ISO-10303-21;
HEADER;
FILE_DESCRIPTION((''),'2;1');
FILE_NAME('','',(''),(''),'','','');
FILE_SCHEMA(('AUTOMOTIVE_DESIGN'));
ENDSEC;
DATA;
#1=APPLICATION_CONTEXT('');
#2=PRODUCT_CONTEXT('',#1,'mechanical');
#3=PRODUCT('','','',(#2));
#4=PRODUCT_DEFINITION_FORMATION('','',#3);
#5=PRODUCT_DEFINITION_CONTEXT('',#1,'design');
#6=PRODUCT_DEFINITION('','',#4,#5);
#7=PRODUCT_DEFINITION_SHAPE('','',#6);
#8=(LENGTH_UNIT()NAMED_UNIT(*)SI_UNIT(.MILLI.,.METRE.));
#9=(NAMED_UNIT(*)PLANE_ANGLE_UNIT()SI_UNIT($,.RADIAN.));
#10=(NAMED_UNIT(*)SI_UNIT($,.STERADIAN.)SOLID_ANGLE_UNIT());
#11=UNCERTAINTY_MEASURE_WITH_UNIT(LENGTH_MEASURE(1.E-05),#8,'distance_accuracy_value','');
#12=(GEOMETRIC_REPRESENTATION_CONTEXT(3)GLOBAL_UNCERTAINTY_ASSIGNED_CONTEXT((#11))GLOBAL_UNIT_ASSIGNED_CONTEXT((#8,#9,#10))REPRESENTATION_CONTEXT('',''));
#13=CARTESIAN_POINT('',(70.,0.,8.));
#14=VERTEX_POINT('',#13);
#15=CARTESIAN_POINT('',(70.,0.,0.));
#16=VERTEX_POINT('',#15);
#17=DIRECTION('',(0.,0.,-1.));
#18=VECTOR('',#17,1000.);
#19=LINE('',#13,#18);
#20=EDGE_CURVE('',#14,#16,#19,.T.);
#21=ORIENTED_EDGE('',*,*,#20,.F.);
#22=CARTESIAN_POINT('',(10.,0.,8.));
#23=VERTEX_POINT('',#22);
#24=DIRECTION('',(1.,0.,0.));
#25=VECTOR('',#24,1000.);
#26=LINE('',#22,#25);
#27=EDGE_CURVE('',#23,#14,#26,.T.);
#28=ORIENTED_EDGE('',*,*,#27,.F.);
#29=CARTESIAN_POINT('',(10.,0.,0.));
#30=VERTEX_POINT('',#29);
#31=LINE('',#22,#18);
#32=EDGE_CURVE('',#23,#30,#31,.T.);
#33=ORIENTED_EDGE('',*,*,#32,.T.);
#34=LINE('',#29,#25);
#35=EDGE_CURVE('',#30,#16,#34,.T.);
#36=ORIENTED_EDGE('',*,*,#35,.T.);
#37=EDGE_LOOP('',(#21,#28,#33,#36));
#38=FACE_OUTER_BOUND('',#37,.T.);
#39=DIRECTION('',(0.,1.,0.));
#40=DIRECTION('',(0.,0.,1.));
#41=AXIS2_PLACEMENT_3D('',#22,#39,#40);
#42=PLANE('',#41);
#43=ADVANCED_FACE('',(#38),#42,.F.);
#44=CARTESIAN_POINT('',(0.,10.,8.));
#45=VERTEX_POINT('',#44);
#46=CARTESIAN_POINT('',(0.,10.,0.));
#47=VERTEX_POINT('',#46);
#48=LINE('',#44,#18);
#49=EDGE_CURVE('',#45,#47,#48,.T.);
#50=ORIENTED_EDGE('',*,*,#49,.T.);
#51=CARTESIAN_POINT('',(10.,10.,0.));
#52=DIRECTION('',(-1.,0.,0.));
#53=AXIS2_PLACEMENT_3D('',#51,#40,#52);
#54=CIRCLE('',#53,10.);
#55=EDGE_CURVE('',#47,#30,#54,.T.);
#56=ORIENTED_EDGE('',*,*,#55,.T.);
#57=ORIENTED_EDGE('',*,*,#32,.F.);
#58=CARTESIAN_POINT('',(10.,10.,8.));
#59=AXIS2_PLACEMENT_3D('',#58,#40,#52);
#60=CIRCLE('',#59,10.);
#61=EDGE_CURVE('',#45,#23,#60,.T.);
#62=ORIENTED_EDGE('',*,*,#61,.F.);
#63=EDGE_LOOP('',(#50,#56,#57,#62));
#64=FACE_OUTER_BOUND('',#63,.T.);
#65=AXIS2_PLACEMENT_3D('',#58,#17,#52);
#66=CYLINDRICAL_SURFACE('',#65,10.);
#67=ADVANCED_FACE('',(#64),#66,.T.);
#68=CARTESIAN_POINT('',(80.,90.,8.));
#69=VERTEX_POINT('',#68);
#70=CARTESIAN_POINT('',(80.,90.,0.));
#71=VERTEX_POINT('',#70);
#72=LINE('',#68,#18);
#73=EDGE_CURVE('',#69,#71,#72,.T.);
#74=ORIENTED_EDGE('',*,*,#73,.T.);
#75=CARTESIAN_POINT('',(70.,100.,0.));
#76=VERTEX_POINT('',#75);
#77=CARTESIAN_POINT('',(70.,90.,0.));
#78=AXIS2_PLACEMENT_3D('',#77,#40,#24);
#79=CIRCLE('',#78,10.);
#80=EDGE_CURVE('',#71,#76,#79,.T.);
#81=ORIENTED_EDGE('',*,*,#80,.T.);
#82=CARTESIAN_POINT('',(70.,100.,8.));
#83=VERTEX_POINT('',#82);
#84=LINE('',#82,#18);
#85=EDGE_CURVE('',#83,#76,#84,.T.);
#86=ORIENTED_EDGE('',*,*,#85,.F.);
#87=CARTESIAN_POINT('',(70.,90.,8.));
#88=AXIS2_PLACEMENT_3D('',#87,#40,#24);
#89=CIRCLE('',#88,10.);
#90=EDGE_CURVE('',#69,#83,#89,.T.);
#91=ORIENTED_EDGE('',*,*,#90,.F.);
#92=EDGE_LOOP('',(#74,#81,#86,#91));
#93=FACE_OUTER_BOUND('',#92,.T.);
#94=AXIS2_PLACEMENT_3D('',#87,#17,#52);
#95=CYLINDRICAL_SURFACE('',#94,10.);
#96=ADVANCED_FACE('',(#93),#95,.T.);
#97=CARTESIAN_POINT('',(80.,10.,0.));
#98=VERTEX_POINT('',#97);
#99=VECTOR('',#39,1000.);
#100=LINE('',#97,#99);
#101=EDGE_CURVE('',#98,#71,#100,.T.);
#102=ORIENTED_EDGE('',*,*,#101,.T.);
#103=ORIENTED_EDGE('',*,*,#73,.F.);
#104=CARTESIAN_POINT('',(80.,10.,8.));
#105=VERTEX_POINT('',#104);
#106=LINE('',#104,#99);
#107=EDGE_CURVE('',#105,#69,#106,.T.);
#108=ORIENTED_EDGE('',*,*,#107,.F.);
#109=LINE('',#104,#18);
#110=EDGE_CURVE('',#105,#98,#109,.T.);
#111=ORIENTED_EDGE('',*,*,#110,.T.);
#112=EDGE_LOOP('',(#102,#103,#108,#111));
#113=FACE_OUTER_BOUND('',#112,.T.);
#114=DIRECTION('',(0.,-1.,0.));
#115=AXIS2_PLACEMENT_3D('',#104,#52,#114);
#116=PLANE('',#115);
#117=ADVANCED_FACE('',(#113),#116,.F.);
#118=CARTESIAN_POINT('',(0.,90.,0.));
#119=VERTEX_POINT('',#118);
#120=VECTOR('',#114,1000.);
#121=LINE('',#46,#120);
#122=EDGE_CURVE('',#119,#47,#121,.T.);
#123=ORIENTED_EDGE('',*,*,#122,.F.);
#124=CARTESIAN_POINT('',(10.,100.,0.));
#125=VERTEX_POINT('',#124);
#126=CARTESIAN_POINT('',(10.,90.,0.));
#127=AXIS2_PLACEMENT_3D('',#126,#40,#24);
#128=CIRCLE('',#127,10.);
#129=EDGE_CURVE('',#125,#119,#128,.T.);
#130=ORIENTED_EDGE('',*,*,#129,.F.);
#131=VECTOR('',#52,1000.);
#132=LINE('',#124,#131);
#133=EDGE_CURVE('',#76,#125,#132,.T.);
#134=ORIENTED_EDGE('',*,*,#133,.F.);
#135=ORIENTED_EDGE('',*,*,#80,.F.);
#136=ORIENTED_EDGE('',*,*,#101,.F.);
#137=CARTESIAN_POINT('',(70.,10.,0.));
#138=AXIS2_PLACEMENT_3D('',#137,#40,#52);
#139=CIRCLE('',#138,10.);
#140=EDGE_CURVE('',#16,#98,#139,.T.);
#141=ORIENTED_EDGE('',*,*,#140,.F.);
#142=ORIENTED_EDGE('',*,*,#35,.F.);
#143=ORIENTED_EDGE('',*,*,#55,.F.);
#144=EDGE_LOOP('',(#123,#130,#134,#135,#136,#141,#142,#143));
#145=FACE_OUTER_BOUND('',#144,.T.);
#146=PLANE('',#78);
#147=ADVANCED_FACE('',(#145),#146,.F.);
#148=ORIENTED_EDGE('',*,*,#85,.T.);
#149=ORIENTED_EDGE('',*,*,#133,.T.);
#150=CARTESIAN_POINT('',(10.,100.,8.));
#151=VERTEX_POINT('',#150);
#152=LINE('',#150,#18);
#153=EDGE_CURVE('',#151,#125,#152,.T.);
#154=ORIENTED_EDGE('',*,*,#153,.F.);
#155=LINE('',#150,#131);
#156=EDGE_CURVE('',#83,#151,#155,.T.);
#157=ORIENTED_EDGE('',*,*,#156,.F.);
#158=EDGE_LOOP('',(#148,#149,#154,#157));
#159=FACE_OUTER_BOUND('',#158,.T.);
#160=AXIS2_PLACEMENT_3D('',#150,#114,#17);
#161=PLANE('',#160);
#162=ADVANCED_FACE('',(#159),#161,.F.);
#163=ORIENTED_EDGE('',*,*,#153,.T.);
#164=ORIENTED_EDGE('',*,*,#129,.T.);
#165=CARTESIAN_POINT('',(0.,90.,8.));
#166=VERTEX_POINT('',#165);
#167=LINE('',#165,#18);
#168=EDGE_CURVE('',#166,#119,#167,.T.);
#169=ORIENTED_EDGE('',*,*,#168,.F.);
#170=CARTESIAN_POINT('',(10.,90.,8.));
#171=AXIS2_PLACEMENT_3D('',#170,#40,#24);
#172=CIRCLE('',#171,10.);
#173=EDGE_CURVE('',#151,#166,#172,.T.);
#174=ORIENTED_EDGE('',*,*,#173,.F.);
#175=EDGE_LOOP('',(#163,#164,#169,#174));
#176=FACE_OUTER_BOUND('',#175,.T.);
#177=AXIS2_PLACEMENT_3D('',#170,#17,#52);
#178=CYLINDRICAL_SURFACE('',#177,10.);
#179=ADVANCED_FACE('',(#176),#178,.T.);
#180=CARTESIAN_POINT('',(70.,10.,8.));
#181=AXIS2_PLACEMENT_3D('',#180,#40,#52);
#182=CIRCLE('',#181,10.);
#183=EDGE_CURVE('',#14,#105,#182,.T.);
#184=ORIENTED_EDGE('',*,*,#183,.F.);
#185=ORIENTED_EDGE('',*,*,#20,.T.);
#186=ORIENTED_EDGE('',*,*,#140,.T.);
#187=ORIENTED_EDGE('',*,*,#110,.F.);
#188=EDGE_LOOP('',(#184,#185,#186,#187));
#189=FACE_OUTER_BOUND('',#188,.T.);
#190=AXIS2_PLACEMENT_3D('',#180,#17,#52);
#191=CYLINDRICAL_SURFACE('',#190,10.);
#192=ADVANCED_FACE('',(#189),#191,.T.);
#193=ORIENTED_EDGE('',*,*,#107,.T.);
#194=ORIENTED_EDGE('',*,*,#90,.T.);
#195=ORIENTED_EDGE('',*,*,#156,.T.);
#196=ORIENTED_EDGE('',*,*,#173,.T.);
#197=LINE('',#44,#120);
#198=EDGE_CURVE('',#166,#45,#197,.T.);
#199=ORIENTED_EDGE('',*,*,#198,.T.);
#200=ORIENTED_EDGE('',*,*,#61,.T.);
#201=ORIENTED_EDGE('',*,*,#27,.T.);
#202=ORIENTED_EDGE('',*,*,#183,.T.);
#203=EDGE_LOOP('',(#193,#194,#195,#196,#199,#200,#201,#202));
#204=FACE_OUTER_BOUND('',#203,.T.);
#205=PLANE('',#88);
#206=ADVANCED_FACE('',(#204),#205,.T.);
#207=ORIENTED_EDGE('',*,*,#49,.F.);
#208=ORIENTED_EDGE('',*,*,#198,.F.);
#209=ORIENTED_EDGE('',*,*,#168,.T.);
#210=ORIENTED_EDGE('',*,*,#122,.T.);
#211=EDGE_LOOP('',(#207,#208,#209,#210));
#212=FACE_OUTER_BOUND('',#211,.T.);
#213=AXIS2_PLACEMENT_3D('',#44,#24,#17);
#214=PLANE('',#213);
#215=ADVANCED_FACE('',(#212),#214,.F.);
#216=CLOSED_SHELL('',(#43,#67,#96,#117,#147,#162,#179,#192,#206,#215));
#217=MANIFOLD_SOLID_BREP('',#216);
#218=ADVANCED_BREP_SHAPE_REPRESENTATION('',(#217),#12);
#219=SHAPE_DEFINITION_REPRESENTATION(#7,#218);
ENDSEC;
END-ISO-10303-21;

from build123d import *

# Parameters (mm, degrees)
BOSS_EXTRUDE1_DEPTH = 8


with BuildPart() as part:
    # Sketch1 → Boss-Extrude1 (new body)
    with BuildSketch(Plane.XY):
        with BuildLine():
            Line((10, 0), (70, 0))
            ThreePointArc((70, 0), (77.071067812, 2.928932188), (80, 10))
            Line((80, 10), (80, 90))
            ThreePointArc((80, 90), (77.071067812, 97.071067812), (70, 100))
            Line((70, 100), (10, 100))
            ThreePointArc((10, 100), (2.928932188, 97.071067812), (0, 90))
            Line((0, 90), (0, 10))
            ThreePointArc((0, 10), (2.928932188, 2.928932188), (10, 0))
        make_face()
    extrude(amount=BOSS_EXTRUDE1_DEPTH)


solid = part.part
